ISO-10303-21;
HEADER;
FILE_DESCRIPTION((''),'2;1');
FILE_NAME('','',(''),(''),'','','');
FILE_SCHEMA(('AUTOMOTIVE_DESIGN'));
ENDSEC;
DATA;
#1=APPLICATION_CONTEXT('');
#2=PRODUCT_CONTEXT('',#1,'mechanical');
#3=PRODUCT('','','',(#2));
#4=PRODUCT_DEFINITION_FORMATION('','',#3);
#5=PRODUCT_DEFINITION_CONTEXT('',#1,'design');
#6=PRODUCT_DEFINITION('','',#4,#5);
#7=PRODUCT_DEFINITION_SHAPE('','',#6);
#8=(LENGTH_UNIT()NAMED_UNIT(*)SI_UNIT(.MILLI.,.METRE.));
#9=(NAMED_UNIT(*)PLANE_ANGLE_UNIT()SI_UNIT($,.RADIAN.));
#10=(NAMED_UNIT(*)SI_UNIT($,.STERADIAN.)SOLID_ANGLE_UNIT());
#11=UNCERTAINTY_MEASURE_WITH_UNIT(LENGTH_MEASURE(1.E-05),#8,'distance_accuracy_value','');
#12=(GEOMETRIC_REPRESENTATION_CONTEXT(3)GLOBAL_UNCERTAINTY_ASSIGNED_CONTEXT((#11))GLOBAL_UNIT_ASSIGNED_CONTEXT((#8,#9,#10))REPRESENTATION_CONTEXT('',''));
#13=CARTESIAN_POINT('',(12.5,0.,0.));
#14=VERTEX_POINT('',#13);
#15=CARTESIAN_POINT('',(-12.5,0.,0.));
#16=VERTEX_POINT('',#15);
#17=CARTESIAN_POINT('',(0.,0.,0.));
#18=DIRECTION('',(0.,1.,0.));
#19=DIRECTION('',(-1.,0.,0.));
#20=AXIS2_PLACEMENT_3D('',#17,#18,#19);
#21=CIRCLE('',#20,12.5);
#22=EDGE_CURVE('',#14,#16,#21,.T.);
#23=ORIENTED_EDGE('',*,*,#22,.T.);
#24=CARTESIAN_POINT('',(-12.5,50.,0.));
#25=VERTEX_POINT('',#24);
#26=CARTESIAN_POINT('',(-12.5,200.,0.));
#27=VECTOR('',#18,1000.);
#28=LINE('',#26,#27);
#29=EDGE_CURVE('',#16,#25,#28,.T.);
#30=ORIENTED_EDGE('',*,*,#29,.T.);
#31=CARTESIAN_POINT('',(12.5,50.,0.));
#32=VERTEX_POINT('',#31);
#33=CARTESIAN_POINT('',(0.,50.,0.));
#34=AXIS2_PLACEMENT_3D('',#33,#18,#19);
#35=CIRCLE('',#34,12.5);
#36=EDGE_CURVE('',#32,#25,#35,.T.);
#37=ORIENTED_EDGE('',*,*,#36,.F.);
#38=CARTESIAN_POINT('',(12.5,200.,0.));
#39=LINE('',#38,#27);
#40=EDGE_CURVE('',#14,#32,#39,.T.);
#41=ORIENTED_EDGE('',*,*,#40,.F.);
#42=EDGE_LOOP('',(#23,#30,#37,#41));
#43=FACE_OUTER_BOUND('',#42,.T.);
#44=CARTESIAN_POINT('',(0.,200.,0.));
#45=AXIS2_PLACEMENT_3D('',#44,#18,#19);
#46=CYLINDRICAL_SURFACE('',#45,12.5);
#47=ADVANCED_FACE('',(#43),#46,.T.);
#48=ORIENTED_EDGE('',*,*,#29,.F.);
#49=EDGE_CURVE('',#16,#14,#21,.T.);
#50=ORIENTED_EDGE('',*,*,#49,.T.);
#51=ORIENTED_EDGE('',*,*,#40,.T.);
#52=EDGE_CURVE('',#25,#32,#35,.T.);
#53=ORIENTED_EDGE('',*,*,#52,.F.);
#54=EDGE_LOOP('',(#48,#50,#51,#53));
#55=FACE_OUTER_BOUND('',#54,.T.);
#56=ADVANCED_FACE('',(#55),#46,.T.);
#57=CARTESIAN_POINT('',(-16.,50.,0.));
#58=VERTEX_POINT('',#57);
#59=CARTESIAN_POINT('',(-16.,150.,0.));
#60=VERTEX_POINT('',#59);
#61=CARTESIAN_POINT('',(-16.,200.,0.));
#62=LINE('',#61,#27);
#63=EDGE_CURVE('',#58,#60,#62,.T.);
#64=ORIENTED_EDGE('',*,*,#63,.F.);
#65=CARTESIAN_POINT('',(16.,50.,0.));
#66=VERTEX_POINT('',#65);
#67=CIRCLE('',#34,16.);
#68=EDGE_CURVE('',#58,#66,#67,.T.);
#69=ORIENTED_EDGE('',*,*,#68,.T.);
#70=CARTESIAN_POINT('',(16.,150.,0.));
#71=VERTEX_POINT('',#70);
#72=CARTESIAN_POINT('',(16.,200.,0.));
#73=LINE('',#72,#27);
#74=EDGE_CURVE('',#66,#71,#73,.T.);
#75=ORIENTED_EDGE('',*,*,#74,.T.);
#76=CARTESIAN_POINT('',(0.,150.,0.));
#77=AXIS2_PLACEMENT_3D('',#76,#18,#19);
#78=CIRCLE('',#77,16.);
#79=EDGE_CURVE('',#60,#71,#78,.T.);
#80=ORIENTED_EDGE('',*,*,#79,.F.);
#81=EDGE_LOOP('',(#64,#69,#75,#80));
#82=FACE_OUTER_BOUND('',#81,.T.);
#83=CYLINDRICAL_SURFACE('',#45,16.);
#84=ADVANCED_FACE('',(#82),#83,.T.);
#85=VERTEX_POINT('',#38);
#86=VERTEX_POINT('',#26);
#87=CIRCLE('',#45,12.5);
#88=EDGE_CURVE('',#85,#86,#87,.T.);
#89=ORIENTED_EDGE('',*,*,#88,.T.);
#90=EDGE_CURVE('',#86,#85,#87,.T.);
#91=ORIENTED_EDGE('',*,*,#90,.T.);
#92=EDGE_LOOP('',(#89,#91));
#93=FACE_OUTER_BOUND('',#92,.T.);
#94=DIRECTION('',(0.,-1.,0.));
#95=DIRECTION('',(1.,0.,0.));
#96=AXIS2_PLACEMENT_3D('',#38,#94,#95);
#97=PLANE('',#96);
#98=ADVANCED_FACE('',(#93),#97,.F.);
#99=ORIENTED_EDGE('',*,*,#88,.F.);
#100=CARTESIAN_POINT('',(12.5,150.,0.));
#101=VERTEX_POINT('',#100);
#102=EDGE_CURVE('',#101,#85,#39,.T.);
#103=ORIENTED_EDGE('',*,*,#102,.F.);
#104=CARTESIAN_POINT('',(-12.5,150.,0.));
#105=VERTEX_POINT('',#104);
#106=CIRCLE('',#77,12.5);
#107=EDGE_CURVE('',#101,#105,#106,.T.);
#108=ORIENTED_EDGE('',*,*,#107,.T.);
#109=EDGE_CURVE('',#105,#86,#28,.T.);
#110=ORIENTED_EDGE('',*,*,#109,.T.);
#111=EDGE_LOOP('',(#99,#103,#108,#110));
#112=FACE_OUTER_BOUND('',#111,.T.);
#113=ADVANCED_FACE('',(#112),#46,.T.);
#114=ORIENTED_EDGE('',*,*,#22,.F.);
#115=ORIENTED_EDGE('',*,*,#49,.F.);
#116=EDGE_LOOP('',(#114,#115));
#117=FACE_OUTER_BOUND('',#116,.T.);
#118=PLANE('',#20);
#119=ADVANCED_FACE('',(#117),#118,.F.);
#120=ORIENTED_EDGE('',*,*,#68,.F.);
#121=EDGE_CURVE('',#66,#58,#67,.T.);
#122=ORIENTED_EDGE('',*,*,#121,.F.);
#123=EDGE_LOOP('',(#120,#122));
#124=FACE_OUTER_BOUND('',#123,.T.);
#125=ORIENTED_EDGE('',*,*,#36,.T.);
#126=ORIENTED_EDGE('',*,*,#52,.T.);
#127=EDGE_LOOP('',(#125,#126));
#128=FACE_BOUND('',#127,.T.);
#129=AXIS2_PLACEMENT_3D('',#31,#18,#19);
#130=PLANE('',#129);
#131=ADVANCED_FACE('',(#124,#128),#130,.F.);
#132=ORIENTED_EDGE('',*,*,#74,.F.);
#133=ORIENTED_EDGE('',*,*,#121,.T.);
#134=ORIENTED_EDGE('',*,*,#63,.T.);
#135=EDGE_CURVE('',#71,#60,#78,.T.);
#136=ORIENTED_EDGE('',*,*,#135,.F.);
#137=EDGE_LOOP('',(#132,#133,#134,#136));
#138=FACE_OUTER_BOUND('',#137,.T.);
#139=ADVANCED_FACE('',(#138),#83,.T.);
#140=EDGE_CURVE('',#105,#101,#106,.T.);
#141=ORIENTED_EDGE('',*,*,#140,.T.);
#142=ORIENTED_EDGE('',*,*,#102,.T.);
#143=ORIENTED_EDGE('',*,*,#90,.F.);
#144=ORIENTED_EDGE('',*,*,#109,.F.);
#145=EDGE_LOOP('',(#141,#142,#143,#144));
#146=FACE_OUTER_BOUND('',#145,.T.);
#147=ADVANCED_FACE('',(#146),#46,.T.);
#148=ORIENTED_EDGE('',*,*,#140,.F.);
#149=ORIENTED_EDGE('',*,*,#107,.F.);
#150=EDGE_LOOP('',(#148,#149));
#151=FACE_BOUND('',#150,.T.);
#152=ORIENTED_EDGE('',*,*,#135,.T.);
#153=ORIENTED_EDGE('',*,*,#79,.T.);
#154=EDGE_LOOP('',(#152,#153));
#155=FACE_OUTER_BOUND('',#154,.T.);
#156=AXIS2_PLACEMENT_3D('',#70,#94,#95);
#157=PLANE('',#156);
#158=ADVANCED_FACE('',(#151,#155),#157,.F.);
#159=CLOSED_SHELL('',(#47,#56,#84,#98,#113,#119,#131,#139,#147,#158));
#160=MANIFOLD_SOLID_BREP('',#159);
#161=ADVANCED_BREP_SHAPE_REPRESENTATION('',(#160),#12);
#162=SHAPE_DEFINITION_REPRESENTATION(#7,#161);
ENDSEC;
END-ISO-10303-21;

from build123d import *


with BuildPart() as part:
    # Pin Profile Sketch → Pin Body Revolve (revolve)
    with BuildSketch(Plane.XY, mode=Mode.PRIVATE) as pin_body_revolve_sk:
        Polygon((0, 0), (12.5, 0), (12.5, 50), (16, 50), (16, 150), (12.5, 150), (12.5, 200), (0, 200), align=None)
    revolve(pin_body_revolve_sk.sketch.rotate(Axis((0, 200, 0), (0, -1, 0)), 180), axis=Axis((0, 200, 0), (0, -1, 0)))


solid = part.part
